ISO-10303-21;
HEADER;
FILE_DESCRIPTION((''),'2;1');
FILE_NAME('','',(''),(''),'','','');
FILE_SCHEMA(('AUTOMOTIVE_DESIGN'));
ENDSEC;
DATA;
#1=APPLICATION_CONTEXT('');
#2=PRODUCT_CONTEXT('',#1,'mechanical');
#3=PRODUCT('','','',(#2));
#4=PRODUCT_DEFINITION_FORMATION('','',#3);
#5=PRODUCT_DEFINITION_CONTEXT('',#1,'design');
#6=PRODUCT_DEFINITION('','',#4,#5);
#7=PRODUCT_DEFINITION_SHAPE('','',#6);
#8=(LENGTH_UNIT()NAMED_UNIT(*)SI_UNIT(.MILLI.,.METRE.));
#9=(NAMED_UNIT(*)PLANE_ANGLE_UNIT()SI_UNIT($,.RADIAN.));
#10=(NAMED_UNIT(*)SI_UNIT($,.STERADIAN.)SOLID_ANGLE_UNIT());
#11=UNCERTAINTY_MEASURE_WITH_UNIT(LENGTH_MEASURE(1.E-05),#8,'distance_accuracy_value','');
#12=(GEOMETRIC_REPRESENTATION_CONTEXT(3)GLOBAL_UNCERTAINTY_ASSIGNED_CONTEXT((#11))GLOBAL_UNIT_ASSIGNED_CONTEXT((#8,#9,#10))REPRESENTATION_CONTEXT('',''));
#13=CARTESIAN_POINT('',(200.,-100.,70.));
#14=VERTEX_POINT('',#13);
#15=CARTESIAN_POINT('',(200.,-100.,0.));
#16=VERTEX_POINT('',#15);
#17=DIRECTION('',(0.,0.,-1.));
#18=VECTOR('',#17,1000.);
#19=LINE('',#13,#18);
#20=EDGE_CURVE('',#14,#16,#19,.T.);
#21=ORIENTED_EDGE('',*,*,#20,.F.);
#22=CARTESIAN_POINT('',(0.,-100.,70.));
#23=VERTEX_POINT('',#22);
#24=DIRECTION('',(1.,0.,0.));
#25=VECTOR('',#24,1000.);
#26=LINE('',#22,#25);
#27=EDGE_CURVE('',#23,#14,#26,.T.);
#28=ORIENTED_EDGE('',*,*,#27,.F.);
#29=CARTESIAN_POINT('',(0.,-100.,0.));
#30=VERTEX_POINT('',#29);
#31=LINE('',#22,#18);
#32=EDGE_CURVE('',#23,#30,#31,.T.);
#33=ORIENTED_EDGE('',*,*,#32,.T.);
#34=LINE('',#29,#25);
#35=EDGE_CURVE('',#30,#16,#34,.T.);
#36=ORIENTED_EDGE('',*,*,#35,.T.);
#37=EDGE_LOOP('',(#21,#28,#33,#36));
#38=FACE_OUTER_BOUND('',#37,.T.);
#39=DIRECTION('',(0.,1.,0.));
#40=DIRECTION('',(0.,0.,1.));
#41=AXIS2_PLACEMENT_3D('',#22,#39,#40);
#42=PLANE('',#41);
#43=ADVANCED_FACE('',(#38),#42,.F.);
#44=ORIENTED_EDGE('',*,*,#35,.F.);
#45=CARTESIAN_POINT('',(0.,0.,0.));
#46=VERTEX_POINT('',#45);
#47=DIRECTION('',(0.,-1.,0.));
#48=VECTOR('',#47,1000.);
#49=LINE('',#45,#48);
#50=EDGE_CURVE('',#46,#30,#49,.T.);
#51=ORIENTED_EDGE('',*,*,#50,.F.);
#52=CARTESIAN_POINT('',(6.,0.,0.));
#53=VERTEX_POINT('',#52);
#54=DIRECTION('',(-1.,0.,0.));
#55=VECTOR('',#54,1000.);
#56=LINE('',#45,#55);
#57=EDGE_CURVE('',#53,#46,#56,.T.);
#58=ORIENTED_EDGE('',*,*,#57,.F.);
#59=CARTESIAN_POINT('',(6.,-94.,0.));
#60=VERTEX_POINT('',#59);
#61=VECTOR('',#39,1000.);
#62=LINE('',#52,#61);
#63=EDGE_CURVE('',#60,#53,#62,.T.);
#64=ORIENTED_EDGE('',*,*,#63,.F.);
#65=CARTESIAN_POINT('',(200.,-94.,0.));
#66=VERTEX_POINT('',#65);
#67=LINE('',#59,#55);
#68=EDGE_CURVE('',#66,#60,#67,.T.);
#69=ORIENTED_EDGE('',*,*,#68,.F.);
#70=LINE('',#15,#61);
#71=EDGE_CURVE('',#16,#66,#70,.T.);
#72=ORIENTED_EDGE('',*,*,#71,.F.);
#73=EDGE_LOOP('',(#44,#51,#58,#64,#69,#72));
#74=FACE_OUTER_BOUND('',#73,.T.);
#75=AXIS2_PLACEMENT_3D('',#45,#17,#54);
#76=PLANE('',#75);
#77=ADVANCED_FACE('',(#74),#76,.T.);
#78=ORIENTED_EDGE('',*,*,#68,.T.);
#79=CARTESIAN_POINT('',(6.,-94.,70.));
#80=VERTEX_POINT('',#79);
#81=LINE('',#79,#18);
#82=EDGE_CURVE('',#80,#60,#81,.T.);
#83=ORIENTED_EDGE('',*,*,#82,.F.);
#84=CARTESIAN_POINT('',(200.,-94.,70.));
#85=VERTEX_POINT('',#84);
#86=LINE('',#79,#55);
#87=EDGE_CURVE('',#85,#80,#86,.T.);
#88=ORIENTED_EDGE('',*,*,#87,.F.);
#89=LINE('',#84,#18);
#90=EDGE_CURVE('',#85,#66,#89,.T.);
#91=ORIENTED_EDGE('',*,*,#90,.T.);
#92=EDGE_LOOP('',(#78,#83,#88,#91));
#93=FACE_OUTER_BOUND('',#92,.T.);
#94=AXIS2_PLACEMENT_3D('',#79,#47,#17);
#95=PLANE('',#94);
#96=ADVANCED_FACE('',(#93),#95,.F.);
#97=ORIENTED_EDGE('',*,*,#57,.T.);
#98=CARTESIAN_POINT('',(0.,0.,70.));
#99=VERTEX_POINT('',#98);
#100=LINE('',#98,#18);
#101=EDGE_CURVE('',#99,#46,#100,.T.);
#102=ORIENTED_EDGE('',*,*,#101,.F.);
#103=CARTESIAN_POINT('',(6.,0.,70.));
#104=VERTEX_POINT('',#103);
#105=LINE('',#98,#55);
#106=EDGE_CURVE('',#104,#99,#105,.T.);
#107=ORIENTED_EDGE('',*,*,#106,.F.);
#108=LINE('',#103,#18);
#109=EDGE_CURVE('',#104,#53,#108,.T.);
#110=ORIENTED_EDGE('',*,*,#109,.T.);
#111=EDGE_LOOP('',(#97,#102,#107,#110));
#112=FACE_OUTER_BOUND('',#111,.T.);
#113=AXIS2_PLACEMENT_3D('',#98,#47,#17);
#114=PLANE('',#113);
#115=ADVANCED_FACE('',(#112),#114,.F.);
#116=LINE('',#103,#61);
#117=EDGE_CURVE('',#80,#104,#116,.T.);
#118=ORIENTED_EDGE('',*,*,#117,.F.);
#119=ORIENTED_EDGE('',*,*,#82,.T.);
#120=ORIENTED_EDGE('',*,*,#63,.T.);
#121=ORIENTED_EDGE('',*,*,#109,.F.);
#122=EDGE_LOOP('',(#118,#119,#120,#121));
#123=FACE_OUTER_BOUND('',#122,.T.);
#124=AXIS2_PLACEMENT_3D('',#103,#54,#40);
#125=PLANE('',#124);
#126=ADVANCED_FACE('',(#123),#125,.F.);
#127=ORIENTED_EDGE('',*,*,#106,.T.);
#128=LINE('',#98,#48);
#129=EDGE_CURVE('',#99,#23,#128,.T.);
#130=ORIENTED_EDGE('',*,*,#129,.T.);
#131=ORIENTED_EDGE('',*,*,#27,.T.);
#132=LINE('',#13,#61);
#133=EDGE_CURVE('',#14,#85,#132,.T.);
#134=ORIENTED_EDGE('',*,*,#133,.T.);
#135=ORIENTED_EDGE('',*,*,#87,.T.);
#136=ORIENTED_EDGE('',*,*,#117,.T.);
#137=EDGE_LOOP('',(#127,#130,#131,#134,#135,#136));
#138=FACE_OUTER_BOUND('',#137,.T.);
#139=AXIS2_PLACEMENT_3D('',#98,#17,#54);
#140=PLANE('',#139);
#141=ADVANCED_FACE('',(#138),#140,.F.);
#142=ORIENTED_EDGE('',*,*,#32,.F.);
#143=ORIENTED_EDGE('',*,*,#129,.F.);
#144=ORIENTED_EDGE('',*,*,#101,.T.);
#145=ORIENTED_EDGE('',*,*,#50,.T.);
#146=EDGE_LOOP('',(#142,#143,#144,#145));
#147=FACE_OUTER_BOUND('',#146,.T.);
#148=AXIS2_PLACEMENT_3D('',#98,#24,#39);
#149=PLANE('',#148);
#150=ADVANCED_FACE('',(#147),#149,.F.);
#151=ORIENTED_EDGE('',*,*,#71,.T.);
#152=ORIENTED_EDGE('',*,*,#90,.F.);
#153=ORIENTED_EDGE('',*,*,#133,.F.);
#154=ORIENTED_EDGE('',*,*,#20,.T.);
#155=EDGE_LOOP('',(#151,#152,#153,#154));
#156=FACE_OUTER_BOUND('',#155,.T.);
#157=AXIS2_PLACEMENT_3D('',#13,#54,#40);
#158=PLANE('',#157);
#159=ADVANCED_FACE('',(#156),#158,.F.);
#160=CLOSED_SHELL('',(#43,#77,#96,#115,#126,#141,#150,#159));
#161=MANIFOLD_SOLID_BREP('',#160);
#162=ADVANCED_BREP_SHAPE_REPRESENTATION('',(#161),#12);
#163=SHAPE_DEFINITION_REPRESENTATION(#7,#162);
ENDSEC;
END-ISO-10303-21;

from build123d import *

# Parameters (mm, degrees)
EXTRUDE_1_DEPTH = 70


with BuildPart() as part:
    # 草图1 → 凸台-拉伸1 (new body)
    with BuildSketch(Plane.XY):
        Polygon((0, 0), (0, -100), (200, -100), (200, -94), (6, -94), (6, 0), align=None)
    extrude(amount=EXTRUDE_1_DEPTH)


solid = part.part
